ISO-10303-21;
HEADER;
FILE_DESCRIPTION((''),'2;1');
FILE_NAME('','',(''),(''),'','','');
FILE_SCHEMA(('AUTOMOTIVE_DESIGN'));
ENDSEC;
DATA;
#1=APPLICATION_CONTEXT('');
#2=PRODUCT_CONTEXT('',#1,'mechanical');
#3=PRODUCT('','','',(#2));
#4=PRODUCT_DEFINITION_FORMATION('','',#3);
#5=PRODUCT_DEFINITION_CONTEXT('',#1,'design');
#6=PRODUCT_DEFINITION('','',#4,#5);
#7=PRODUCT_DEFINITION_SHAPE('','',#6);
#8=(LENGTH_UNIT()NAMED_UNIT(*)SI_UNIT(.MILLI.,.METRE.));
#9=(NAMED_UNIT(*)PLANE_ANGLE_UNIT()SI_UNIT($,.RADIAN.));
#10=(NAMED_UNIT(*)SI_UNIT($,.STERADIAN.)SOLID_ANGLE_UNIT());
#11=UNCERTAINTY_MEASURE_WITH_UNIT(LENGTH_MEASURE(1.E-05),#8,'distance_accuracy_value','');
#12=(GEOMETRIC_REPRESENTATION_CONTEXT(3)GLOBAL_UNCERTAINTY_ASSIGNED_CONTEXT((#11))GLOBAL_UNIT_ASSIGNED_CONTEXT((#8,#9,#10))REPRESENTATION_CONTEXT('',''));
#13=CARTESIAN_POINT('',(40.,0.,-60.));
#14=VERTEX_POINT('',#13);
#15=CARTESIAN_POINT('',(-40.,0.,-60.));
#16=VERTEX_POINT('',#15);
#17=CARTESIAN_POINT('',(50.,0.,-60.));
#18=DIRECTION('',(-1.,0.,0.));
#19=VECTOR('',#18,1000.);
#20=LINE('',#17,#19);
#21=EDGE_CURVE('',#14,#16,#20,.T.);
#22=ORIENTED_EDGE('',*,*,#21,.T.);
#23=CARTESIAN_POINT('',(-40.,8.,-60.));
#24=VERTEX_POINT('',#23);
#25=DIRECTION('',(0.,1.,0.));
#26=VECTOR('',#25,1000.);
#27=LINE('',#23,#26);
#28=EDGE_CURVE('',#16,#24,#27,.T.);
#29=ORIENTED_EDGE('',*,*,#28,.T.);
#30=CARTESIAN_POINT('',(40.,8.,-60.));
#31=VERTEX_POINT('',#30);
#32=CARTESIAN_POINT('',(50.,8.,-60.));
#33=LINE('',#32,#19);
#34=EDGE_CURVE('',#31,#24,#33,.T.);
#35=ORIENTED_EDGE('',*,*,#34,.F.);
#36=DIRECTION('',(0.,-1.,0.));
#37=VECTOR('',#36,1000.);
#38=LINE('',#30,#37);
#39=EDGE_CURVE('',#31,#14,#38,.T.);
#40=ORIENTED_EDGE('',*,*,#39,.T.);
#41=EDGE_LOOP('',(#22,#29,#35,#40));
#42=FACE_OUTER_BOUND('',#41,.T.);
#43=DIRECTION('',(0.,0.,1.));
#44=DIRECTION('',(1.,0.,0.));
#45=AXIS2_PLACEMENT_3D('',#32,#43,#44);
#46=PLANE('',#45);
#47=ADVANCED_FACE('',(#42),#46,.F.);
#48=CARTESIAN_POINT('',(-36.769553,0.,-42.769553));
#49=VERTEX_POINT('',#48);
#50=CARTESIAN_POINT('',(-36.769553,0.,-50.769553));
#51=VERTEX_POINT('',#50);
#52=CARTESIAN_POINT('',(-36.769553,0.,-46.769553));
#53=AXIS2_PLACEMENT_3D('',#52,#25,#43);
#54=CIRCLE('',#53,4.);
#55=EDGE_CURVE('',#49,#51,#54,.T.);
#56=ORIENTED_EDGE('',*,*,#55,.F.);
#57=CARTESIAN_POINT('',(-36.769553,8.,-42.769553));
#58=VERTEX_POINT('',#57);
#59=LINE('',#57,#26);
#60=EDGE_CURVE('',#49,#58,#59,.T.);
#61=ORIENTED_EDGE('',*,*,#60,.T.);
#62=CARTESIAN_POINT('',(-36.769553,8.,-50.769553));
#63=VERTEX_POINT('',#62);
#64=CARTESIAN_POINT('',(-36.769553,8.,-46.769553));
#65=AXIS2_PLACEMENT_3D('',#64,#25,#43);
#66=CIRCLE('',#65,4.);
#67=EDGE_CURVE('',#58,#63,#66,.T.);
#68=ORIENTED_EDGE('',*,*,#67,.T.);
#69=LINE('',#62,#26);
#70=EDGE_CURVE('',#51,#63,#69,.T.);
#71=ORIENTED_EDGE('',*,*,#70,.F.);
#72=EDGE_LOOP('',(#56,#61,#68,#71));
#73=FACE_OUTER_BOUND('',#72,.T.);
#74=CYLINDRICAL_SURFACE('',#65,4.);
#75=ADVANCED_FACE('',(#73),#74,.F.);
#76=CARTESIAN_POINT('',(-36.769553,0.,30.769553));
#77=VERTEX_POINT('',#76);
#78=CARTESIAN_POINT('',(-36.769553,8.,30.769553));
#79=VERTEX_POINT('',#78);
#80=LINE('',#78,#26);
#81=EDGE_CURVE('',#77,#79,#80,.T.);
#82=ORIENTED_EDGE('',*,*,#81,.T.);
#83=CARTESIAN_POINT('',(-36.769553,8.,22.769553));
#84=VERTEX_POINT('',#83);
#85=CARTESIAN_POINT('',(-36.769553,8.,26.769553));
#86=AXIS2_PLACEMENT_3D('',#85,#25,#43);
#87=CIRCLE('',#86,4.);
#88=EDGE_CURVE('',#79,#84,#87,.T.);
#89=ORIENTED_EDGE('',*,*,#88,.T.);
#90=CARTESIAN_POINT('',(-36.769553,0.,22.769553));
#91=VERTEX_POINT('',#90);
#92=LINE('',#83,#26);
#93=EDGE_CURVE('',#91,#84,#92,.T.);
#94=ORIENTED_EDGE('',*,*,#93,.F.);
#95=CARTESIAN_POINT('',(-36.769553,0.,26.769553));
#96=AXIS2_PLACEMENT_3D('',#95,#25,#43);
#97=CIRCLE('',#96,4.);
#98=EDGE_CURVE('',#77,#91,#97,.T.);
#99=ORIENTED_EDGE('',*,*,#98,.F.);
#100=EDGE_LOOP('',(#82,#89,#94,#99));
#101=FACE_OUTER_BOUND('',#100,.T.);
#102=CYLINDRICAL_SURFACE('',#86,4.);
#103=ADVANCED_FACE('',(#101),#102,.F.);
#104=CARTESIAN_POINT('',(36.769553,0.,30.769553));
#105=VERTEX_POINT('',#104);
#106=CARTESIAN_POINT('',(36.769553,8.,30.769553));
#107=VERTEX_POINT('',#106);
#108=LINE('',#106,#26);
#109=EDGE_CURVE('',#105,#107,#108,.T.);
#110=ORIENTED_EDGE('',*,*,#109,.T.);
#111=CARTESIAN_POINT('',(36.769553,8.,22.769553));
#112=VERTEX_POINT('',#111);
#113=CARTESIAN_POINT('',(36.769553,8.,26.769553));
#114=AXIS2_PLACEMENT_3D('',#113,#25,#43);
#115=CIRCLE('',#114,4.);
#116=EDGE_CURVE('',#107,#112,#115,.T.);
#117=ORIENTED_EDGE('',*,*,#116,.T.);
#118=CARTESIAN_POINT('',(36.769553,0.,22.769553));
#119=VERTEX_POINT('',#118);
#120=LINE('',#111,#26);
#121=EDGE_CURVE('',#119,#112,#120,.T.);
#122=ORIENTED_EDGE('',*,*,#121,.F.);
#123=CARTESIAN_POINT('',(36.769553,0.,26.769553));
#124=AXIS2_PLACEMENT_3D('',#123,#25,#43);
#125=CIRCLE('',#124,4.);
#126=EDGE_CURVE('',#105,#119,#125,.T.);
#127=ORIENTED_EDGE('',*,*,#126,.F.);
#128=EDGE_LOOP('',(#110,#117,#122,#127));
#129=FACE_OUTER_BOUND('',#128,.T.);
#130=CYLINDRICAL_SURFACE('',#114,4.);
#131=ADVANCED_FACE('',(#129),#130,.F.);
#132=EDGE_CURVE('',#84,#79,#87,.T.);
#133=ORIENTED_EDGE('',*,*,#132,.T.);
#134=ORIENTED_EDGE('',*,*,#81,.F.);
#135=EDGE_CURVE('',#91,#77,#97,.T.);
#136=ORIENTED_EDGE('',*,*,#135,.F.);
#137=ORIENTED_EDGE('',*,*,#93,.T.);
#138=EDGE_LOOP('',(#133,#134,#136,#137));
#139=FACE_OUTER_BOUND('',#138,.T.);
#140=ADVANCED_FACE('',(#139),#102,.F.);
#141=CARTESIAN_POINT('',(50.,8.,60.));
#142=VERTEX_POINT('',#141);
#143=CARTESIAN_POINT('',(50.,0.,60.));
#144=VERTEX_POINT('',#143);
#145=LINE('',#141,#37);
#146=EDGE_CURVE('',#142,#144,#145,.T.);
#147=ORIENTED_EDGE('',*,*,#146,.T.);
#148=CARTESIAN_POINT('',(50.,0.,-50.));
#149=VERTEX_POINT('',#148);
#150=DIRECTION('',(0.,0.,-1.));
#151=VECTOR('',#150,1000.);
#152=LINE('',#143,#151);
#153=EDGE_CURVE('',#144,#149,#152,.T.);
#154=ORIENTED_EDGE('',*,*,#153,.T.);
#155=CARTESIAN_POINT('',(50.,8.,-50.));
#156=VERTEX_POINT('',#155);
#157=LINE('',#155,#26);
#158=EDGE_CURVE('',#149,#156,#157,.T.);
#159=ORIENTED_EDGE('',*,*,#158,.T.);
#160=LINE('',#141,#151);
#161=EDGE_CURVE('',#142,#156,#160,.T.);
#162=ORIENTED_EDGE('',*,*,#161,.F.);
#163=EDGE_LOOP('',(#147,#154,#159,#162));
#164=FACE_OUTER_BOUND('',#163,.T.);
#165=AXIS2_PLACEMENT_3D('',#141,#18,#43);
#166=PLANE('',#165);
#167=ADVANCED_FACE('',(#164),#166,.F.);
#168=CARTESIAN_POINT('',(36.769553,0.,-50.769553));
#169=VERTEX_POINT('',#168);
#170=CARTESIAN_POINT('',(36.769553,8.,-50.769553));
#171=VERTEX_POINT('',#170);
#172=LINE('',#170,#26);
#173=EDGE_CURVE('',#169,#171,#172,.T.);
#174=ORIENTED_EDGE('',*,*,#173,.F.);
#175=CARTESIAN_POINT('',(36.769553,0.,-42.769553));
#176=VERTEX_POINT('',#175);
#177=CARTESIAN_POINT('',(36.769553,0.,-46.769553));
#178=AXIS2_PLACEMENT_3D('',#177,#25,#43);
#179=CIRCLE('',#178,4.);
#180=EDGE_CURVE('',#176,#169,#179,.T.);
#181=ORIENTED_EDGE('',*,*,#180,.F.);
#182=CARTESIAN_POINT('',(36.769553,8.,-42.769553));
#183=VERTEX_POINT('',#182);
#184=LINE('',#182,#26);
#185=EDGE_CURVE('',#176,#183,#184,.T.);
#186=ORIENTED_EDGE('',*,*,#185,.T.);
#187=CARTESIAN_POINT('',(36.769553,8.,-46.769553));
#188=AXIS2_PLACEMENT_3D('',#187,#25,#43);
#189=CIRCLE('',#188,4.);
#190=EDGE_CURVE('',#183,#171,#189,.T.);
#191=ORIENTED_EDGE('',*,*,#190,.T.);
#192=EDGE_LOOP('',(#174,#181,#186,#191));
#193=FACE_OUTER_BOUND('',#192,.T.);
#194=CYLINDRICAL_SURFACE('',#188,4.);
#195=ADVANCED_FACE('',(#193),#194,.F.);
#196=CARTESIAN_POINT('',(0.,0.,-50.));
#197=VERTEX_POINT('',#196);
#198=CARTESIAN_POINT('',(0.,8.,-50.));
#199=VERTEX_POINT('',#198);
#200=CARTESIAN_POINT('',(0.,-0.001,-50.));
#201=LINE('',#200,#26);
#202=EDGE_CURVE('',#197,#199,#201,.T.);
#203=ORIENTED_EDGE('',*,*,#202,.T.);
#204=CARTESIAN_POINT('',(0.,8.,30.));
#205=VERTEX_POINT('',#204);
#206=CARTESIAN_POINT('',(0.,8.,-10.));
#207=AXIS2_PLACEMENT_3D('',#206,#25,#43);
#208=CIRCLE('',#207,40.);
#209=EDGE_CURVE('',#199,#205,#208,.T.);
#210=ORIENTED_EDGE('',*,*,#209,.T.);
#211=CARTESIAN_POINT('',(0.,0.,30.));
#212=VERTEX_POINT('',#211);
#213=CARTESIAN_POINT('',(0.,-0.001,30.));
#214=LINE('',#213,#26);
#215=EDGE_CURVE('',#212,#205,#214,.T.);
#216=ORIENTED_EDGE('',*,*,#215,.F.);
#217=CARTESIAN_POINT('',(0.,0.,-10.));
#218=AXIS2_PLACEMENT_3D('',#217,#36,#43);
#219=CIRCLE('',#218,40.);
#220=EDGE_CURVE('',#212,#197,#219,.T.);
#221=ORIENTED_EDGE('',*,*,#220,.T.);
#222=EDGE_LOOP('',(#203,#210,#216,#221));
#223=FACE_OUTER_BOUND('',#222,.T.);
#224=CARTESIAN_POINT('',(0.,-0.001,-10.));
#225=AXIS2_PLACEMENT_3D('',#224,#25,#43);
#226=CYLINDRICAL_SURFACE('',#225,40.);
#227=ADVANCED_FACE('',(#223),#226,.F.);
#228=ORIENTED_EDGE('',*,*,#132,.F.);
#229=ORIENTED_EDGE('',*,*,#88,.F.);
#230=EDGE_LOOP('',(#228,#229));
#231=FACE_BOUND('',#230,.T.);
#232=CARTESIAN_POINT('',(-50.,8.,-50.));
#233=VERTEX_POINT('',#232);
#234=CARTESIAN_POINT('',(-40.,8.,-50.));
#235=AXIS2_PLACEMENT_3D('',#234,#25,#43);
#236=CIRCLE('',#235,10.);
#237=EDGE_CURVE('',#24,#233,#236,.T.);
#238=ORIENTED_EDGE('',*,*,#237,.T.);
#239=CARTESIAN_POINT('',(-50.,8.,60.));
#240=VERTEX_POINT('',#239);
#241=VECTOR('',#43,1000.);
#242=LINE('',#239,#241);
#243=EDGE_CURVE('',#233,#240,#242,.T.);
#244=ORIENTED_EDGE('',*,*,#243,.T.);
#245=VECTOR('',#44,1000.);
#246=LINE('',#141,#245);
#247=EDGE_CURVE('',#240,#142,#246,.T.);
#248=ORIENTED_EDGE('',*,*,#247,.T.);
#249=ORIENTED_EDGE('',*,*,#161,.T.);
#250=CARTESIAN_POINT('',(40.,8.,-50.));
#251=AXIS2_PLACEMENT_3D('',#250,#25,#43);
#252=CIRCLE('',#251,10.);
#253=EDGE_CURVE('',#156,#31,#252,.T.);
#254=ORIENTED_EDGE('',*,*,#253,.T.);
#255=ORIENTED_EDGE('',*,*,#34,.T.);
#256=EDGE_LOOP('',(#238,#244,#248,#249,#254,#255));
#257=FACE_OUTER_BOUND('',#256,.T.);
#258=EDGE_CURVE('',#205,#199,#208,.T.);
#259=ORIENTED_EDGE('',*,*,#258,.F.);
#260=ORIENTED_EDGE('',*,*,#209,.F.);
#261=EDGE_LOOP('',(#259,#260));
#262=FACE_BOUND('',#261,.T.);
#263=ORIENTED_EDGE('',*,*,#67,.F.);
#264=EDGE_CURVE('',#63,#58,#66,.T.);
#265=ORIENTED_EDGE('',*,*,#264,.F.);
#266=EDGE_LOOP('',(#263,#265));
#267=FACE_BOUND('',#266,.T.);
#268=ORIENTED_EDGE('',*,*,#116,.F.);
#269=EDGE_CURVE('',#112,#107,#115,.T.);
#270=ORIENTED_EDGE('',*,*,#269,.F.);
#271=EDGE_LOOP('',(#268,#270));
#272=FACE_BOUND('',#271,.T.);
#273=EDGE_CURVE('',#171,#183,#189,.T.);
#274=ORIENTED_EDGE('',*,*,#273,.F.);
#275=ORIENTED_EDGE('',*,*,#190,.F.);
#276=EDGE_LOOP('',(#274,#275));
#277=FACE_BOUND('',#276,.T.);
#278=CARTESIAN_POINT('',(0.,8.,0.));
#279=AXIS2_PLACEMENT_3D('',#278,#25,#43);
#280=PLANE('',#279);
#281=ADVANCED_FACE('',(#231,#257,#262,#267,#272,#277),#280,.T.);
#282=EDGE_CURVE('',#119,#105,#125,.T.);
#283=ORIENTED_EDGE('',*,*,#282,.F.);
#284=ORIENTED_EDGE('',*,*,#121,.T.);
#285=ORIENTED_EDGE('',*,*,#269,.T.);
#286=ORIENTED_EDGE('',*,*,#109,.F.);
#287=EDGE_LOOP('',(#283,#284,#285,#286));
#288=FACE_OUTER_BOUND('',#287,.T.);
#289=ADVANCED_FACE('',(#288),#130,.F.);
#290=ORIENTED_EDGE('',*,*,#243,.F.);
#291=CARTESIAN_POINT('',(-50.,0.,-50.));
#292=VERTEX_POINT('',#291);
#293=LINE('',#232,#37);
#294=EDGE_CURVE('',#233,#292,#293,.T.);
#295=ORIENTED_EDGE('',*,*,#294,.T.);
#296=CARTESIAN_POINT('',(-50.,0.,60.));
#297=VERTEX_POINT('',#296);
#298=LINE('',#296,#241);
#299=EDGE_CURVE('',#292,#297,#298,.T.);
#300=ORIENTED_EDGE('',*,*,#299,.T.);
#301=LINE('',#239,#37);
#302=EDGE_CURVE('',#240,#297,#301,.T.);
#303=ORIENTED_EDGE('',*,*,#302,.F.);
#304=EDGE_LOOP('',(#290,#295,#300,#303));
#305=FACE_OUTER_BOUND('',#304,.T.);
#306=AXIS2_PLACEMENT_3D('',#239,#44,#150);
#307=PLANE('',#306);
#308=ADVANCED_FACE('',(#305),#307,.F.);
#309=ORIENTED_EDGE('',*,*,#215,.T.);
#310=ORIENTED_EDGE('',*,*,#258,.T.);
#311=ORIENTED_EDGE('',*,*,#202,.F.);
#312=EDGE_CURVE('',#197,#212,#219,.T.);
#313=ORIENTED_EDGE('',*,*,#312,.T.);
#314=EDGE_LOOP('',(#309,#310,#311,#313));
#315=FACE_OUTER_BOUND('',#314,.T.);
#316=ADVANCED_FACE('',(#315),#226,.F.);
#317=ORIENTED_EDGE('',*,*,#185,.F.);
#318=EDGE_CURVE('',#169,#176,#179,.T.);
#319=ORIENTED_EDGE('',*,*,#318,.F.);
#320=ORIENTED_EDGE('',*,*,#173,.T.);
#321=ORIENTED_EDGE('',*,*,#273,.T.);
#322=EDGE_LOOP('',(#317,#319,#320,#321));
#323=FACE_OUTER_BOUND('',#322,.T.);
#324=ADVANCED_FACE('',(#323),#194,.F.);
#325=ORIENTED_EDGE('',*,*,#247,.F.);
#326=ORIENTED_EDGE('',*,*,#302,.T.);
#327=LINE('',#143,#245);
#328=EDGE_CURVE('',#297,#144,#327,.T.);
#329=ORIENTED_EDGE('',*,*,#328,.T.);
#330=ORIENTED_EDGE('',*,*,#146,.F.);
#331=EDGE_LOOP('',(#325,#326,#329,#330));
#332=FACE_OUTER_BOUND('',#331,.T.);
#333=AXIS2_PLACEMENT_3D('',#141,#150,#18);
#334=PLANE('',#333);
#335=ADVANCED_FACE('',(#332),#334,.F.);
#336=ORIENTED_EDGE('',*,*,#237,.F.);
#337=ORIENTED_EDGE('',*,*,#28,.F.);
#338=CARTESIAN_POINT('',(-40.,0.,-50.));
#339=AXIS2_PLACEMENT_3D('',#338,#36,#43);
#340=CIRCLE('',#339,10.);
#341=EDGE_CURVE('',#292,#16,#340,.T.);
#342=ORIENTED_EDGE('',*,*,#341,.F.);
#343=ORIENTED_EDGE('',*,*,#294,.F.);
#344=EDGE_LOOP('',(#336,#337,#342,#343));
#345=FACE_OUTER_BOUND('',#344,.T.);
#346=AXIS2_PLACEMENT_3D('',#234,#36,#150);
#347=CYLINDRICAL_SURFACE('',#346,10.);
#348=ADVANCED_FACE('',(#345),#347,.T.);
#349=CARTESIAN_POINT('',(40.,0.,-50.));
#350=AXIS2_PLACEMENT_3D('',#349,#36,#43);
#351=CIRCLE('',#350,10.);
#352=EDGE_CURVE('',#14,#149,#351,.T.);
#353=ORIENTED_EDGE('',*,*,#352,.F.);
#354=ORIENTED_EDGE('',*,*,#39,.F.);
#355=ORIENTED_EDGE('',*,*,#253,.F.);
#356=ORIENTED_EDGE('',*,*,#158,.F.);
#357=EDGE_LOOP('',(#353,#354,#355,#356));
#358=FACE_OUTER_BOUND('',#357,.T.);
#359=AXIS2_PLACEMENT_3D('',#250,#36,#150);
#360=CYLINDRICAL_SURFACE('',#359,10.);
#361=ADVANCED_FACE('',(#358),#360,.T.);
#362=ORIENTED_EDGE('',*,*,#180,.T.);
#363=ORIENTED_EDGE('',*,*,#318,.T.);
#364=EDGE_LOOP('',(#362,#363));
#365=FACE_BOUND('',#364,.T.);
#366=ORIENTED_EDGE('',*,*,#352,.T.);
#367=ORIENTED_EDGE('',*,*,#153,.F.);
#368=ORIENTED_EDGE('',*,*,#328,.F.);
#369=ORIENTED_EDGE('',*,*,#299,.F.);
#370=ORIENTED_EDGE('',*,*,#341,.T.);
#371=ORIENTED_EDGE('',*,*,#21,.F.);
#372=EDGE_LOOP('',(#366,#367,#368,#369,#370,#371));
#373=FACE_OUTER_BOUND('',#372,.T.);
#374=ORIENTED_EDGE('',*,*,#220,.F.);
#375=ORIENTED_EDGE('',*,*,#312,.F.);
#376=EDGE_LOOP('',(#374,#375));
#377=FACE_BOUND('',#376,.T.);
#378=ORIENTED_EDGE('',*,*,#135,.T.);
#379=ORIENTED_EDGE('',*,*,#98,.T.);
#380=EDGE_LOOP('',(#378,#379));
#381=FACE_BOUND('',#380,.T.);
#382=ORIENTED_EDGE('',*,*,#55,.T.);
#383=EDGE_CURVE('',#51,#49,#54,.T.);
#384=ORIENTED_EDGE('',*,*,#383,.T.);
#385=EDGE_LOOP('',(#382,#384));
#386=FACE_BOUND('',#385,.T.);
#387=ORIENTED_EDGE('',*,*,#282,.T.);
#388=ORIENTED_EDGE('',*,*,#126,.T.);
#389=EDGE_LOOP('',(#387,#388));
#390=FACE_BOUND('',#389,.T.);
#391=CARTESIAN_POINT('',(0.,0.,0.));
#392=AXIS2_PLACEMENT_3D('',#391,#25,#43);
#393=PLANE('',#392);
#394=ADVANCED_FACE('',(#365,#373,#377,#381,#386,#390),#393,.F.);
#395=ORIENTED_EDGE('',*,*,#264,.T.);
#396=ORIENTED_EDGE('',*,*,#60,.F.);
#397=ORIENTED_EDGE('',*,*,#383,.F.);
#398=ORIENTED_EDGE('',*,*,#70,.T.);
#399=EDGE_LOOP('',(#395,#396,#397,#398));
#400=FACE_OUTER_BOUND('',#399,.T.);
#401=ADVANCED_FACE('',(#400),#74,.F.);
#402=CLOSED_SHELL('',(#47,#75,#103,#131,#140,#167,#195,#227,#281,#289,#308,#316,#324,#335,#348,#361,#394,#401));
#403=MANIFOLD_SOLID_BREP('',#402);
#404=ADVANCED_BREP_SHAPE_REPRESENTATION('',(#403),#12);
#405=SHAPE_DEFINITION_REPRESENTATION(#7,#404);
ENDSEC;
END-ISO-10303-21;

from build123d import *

# Parameters (mm, degrees)
SKETCH1_W                = 100
SKETCH1_H                = 120
BOSS_EXTRUDE1_DEPTH      = 8
FILLET1_R                = 10
CUT_EXTRUDE1_REACH       = 80.511
SKETCH2_R                = 40
F_8_0_8_DIAMETER_HOLE1_D = 8
CIRPATTERN1_COUNT        = 4


with BuildPart() as part:
    # Sketch1 → Boss-Extrude1 (new body)
    with BuildSketch(Plane(origin=(0, 0, 0), x_dir=(1, 0, 0), z_dir=(0, 1, 0))):
        Rectangle(SKETCH1_W, SKETCH1_H)
    extrude(amount=BOSS_EXTRUDE1_DEPTH)

    # Fillet1
    fillet1_edges = [part.edges().sort_by_distance(p)[0] for p in [
        (-50, 4, -60),
        (50, 4, -60),
    ]]
    fillet(fillet1_edges, radius=FILLET1_R)

    # Sketch2 → Cut-Extrude1 (cut, up to next)
    with BuildSketch(Plane(origin=(0, 8, 0), x_dir=(1, 0, 0), z_dir=(0, 1, 0)), mode=Mode.PRIVATE) as cut_extrude1_sk1:
        with Locations(Location((0, 10, 0), (0, 0, 270))):
            Circle(SKETCH2_R)
    cut_extrude1_tool1 = extrude(cut_extrude1_sk1.sketch, amount=-CUT_EXTRUDE1_REACH, mode=Mode.PRIVATE) & part.part
    add(cut_extrude1_tool1.solids().sort_by_distance((0, 8, -10))[0], mode=Mode.SUBTRACT)

    # Ø8.0 (8) Diameter Hole1 (through all)
    with Locations(Plane(origin=(0, 8, 0), x_dir=(1, 0, 0), z_dir=(0, 1, 0))):
        with Locations((-36.769552622, 46.769552622)):
            f_8_0_8_diameter_hole1 = Hole(F_8_0_8_DIAMETER_HOLE1_D / 2)

    # CirPattern1: Ø8.0 (8) Diameter Hole1 ×4 about axis
    cirpattern1_axis = Axis((0, 0, -10), (0, 1, 0))
    for i in range(1, CIRPATTERN1_COUNT):
        add(f_8_0_8_diameter_hole1.rotate(cirpattern1_axis, i * 360 / CIRPATTERN1_COUNT), mode=Mode.SUBTRACT)


solid = part.part
